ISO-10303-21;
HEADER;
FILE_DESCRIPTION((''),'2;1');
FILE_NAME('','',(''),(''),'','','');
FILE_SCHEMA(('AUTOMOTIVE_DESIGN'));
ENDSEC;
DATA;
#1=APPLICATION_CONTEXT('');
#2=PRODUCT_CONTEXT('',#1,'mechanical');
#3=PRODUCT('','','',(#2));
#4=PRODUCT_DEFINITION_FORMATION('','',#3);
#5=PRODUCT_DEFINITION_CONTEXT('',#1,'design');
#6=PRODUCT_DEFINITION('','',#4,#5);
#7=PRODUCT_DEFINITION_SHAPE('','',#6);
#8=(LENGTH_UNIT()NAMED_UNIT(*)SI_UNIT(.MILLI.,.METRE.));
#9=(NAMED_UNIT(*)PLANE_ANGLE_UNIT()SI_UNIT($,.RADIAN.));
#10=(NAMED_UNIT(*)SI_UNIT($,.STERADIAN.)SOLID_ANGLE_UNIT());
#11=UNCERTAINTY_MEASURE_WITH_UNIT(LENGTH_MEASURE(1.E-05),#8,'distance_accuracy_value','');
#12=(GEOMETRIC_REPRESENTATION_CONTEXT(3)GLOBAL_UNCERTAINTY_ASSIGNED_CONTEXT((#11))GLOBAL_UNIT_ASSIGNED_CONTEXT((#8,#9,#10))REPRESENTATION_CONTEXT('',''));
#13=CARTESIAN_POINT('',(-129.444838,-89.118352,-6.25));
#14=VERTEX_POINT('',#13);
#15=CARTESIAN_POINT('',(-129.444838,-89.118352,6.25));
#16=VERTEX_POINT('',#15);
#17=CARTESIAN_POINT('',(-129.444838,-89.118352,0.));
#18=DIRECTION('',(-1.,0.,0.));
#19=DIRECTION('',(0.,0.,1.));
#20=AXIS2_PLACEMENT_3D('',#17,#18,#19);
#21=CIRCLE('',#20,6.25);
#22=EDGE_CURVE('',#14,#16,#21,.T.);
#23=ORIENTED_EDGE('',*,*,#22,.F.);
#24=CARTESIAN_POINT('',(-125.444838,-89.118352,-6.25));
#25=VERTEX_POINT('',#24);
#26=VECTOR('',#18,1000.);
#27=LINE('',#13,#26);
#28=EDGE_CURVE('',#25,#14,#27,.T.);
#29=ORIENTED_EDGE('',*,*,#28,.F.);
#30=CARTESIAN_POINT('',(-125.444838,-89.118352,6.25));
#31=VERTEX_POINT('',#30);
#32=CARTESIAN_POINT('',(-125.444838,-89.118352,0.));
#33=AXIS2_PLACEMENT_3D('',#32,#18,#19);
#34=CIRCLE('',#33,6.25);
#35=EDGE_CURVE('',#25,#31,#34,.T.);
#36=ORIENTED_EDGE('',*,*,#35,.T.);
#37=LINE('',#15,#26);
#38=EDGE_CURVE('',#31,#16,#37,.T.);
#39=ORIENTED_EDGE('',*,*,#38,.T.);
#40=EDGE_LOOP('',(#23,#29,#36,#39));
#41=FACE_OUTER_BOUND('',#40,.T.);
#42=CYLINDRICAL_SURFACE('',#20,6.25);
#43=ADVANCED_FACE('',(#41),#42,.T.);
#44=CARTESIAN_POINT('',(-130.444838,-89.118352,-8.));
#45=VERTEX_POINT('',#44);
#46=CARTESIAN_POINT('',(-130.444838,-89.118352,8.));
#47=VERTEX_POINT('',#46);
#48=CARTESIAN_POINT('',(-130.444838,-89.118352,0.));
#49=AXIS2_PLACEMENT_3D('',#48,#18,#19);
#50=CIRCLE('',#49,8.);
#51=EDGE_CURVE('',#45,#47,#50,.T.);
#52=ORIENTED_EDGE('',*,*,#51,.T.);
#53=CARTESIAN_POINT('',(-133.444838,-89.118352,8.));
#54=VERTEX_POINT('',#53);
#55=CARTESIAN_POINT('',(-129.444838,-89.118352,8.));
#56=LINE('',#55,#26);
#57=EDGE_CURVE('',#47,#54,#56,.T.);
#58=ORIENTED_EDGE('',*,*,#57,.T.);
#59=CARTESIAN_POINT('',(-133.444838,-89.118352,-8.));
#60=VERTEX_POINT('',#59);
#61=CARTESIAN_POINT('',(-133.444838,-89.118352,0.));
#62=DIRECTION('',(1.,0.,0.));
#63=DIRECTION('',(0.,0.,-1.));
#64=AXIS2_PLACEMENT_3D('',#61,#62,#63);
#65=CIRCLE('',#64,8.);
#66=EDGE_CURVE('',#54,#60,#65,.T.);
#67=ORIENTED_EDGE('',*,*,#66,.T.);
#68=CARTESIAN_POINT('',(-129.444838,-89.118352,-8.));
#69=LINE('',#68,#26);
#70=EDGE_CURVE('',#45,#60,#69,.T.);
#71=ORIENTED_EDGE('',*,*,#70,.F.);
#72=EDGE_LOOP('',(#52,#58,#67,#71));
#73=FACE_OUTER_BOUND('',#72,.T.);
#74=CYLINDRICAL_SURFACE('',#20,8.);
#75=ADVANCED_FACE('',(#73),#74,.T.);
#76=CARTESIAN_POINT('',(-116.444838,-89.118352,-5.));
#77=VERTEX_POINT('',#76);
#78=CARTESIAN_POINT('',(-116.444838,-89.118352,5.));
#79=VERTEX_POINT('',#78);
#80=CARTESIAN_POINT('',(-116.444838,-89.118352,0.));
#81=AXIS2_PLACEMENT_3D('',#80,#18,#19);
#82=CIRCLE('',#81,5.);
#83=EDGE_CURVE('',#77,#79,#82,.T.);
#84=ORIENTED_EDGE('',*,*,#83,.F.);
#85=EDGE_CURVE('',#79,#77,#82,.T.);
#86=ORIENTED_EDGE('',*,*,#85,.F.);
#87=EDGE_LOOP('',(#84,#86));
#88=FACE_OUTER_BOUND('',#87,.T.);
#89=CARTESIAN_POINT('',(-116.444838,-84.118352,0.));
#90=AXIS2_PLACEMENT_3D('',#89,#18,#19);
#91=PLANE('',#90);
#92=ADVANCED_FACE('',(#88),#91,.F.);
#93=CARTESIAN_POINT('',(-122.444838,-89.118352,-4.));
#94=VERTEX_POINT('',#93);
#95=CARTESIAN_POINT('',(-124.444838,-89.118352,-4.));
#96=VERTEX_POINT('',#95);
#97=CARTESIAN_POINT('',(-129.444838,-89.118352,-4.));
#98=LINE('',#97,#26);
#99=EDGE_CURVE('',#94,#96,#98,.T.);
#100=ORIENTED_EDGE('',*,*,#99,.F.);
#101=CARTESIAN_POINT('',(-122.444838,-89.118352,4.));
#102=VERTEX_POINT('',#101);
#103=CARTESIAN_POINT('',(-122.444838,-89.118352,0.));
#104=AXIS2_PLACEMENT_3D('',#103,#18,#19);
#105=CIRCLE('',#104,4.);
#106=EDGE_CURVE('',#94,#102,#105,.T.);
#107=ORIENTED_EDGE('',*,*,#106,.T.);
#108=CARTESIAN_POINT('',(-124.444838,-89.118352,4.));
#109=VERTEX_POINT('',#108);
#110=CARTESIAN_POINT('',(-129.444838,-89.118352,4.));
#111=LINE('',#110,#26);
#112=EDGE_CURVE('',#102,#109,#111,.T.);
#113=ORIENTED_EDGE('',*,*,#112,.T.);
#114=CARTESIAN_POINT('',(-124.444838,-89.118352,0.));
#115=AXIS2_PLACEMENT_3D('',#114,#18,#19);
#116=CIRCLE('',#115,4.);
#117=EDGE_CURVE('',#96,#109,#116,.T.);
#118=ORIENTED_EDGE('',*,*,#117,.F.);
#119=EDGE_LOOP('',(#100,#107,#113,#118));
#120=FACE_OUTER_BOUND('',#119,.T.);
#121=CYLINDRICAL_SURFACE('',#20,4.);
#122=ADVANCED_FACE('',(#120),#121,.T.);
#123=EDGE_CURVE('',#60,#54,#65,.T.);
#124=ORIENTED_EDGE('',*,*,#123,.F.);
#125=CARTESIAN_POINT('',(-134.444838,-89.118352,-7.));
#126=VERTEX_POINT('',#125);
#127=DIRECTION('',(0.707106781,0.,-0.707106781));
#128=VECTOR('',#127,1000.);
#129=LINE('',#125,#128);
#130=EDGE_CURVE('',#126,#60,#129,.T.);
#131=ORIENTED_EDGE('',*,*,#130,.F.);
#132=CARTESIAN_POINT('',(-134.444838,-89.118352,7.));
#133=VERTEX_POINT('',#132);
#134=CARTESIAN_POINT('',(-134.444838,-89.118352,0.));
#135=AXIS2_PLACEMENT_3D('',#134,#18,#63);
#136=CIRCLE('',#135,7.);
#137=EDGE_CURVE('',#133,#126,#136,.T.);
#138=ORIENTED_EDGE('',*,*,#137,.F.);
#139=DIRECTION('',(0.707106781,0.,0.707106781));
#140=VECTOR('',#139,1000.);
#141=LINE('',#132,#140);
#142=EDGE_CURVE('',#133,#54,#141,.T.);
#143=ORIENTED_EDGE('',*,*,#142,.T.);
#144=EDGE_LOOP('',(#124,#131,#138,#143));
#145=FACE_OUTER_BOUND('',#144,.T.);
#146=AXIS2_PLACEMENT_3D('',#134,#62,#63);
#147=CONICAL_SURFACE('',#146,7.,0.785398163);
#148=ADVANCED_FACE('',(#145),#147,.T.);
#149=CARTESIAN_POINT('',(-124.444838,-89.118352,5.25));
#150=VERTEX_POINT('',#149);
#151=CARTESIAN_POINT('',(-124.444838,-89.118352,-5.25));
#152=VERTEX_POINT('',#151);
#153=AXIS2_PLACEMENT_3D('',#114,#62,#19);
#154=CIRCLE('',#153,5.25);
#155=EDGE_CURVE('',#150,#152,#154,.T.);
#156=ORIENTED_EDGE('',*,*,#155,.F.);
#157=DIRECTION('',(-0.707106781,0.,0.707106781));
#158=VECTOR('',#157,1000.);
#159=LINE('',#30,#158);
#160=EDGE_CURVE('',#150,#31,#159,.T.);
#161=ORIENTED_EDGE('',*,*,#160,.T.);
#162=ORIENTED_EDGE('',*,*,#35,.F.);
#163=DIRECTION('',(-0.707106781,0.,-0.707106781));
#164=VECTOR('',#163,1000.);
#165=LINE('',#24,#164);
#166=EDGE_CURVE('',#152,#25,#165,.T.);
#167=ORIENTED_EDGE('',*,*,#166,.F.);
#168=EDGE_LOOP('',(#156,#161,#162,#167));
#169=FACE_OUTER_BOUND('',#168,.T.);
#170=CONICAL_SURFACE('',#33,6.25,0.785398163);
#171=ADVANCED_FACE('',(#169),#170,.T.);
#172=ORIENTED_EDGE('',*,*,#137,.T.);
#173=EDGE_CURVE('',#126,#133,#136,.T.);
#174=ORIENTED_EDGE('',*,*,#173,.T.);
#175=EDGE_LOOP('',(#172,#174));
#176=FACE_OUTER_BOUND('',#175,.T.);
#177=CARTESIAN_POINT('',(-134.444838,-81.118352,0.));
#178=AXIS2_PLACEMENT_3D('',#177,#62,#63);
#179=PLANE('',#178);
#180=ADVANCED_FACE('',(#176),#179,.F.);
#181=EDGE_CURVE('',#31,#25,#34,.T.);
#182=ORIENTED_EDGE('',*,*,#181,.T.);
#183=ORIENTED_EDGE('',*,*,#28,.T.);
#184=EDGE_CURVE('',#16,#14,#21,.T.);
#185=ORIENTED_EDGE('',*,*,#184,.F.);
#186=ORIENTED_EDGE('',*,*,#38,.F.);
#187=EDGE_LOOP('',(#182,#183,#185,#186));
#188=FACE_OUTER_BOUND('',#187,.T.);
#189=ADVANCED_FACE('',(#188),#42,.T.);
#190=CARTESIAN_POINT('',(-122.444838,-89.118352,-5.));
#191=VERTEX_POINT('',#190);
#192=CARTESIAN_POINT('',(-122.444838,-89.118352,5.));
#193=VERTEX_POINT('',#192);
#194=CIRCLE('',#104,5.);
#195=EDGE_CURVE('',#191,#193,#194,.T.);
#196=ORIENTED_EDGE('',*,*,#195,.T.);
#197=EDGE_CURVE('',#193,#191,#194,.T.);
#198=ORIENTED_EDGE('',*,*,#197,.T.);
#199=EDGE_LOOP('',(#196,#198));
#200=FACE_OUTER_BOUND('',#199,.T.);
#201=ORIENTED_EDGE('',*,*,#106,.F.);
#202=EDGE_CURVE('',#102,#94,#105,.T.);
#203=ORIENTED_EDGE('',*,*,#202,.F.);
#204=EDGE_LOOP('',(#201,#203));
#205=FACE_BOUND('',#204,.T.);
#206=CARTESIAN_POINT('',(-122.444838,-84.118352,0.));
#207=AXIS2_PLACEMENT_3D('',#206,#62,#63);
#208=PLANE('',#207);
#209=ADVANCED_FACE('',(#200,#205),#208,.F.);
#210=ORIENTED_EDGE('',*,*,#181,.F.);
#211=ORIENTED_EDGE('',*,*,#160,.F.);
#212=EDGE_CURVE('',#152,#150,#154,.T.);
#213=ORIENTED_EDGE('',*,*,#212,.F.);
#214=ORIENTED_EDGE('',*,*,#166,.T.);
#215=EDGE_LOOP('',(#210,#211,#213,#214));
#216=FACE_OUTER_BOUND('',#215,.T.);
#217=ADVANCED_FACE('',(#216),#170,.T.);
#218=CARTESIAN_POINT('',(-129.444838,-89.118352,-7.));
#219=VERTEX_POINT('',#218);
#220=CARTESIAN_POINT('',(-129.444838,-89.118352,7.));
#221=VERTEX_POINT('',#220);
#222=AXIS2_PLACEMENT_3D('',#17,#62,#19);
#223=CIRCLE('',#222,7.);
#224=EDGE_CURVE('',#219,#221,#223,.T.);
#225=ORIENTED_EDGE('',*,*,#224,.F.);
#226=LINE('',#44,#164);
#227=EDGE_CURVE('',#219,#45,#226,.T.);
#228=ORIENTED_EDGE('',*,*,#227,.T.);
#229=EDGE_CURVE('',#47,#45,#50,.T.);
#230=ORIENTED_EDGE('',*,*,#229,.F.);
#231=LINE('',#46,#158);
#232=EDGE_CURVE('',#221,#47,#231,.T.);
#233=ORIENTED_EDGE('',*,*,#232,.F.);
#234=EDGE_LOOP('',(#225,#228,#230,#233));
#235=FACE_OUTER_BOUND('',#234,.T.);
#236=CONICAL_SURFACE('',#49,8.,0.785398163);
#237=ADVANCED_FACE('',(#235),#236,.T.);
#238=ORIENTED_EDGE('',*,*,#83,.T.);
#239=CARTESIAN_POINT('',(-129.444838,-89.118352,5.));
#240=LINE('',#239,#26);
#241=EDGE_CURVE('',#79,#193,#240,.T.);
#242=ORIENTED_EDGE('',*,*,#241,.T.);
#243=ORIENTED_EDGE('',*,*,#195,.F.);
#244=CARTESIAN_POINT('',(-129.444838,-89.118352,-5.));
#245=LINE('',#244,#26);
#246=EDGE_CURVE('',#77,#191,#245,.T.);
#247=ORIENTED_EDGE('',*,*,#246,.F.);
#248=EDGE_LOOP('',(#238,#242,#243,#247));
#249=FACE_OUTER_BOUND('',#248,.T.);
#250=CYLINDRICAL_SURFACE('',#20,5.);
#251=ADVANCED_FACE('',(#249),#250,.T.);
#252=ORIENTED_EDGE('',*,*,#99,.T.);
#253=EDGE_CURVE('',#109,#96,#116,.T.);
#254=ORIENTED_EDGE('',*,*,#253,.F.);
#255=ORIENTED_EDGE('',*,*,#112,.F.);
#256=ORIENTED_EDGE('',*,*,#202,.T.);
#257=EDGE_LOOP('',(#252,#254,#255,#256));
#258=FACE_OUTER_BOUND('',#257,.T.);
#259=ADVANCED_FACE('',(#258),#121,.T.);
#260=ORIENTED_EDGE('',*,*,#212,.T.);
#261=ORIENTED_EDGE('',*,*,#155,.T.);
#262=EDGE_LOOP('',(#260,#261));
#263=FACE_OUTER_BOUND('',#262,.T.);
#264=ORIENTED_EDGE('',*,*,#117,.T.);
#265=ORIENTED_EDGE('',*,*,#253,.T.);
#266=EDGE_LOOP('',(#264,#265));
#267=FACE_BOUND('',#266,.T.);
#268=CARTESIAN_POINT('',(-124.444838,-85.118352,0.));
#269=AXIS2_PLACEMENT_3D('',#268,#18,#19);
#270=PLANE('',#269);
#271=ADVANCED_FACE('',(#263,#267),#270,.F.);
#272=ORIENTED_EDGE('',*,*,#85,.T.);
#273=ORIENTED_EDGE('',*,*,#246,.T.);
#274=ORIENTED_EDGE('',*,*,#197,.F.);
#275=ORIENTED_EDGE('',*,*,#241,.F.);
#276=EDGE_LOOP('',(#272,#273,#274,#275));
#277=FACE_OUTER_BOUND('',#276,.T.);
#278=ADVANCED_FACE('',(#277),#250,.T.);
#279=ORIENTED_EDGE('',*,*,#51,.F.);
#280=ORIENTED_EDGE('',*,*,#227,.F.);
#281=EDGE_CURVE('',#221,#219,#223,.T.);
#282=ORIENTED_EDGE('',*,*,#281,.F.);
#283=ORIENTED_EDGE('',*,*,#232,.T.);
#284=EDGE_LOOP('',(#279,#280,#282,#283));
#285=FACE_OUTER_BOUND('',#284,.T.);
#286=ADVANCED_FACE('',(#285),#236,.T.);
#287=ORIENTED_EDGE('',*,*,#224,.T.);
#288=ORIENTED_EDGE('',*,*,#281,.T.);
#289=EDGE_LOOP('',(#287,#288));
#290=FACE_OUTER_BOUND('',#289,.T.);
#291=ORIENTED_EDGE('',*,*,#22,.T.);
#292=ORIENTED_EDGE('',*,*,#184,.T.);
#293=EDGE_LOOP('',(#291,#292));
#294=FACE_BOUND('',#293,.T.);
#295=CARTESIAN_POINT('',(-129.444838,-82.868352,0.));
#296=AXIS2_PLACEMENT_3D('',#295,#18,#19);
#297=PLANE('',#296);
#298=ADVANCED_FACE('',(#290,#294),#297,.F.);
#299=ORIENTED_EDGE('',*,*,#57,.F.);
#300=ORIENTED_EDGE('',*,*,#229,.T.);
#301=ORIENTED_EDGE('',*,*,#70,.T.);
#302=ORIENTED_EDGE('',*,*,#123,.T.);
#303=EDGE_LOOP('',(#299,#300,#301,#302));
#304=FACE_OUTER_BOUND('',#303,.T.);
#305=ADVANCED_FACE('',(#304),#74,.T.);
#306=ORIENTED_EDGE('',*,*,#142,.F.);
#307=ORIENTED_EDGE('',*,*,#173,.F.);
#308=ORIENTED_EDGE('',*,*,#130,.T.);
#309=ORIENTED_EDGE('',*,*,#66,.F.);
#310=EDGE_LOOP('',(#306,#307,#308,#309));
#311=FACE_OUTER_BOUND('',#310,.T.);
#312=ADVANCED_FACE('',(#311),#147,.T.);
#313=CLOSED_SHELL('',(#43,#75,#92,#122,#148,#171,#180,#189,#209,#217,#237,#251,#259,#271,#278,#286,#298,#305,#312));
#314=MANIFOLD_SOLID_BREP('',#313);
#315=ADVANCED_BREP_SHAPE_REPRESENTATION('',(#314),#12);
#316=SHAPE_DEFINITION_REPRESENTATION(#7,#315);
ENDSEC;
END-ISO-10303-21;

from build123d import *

# Parameters (mm, degrees)
CHAMFER_1_SIZE = 1


with BuildPart() as part:
    # 草图1 → 旋转1 (revolve)
    with BuildSketch(Plane.XY, mode=Mode.PRIVATE) as revolve_1_sk:
        Polygon((-116.444838016, -84.118352239), (-122.444838016, -84.118352239), (-122.444838016, -85.118352239), (-124.444838016, -85.118352239), (-124.444838016, -82.868352239), (-129.444838016, -82.868352239), (-129.444838016, -81.118352239), (-134.444838016, -81.118352239), (-134.444838016, -89.118352239), (-116.444838016, -89.118352239), align=None)
    revolve(revolve_1_sk.sketch.rotate(Axis((-129.444838016, -89.118352239, 0), (1, 0, 0)), 90), axis=Axis((-129.444838016, -89.118352239, 0), (1, 0, 0)))

    # 倒角1
    chamfer_1_edges = [part.edges().sort_by_distance(p)[0] for p in [
        (-124.444838016, -89.118352239, -6.25),
        (-134.444838016, -89.118352239, -8),
        (-129.444838016, -89.118352239, -8),
    ]]
    chamfer(chamfer_1_edges, length=CHAMFER_1_SIZE)


solid = part.part
